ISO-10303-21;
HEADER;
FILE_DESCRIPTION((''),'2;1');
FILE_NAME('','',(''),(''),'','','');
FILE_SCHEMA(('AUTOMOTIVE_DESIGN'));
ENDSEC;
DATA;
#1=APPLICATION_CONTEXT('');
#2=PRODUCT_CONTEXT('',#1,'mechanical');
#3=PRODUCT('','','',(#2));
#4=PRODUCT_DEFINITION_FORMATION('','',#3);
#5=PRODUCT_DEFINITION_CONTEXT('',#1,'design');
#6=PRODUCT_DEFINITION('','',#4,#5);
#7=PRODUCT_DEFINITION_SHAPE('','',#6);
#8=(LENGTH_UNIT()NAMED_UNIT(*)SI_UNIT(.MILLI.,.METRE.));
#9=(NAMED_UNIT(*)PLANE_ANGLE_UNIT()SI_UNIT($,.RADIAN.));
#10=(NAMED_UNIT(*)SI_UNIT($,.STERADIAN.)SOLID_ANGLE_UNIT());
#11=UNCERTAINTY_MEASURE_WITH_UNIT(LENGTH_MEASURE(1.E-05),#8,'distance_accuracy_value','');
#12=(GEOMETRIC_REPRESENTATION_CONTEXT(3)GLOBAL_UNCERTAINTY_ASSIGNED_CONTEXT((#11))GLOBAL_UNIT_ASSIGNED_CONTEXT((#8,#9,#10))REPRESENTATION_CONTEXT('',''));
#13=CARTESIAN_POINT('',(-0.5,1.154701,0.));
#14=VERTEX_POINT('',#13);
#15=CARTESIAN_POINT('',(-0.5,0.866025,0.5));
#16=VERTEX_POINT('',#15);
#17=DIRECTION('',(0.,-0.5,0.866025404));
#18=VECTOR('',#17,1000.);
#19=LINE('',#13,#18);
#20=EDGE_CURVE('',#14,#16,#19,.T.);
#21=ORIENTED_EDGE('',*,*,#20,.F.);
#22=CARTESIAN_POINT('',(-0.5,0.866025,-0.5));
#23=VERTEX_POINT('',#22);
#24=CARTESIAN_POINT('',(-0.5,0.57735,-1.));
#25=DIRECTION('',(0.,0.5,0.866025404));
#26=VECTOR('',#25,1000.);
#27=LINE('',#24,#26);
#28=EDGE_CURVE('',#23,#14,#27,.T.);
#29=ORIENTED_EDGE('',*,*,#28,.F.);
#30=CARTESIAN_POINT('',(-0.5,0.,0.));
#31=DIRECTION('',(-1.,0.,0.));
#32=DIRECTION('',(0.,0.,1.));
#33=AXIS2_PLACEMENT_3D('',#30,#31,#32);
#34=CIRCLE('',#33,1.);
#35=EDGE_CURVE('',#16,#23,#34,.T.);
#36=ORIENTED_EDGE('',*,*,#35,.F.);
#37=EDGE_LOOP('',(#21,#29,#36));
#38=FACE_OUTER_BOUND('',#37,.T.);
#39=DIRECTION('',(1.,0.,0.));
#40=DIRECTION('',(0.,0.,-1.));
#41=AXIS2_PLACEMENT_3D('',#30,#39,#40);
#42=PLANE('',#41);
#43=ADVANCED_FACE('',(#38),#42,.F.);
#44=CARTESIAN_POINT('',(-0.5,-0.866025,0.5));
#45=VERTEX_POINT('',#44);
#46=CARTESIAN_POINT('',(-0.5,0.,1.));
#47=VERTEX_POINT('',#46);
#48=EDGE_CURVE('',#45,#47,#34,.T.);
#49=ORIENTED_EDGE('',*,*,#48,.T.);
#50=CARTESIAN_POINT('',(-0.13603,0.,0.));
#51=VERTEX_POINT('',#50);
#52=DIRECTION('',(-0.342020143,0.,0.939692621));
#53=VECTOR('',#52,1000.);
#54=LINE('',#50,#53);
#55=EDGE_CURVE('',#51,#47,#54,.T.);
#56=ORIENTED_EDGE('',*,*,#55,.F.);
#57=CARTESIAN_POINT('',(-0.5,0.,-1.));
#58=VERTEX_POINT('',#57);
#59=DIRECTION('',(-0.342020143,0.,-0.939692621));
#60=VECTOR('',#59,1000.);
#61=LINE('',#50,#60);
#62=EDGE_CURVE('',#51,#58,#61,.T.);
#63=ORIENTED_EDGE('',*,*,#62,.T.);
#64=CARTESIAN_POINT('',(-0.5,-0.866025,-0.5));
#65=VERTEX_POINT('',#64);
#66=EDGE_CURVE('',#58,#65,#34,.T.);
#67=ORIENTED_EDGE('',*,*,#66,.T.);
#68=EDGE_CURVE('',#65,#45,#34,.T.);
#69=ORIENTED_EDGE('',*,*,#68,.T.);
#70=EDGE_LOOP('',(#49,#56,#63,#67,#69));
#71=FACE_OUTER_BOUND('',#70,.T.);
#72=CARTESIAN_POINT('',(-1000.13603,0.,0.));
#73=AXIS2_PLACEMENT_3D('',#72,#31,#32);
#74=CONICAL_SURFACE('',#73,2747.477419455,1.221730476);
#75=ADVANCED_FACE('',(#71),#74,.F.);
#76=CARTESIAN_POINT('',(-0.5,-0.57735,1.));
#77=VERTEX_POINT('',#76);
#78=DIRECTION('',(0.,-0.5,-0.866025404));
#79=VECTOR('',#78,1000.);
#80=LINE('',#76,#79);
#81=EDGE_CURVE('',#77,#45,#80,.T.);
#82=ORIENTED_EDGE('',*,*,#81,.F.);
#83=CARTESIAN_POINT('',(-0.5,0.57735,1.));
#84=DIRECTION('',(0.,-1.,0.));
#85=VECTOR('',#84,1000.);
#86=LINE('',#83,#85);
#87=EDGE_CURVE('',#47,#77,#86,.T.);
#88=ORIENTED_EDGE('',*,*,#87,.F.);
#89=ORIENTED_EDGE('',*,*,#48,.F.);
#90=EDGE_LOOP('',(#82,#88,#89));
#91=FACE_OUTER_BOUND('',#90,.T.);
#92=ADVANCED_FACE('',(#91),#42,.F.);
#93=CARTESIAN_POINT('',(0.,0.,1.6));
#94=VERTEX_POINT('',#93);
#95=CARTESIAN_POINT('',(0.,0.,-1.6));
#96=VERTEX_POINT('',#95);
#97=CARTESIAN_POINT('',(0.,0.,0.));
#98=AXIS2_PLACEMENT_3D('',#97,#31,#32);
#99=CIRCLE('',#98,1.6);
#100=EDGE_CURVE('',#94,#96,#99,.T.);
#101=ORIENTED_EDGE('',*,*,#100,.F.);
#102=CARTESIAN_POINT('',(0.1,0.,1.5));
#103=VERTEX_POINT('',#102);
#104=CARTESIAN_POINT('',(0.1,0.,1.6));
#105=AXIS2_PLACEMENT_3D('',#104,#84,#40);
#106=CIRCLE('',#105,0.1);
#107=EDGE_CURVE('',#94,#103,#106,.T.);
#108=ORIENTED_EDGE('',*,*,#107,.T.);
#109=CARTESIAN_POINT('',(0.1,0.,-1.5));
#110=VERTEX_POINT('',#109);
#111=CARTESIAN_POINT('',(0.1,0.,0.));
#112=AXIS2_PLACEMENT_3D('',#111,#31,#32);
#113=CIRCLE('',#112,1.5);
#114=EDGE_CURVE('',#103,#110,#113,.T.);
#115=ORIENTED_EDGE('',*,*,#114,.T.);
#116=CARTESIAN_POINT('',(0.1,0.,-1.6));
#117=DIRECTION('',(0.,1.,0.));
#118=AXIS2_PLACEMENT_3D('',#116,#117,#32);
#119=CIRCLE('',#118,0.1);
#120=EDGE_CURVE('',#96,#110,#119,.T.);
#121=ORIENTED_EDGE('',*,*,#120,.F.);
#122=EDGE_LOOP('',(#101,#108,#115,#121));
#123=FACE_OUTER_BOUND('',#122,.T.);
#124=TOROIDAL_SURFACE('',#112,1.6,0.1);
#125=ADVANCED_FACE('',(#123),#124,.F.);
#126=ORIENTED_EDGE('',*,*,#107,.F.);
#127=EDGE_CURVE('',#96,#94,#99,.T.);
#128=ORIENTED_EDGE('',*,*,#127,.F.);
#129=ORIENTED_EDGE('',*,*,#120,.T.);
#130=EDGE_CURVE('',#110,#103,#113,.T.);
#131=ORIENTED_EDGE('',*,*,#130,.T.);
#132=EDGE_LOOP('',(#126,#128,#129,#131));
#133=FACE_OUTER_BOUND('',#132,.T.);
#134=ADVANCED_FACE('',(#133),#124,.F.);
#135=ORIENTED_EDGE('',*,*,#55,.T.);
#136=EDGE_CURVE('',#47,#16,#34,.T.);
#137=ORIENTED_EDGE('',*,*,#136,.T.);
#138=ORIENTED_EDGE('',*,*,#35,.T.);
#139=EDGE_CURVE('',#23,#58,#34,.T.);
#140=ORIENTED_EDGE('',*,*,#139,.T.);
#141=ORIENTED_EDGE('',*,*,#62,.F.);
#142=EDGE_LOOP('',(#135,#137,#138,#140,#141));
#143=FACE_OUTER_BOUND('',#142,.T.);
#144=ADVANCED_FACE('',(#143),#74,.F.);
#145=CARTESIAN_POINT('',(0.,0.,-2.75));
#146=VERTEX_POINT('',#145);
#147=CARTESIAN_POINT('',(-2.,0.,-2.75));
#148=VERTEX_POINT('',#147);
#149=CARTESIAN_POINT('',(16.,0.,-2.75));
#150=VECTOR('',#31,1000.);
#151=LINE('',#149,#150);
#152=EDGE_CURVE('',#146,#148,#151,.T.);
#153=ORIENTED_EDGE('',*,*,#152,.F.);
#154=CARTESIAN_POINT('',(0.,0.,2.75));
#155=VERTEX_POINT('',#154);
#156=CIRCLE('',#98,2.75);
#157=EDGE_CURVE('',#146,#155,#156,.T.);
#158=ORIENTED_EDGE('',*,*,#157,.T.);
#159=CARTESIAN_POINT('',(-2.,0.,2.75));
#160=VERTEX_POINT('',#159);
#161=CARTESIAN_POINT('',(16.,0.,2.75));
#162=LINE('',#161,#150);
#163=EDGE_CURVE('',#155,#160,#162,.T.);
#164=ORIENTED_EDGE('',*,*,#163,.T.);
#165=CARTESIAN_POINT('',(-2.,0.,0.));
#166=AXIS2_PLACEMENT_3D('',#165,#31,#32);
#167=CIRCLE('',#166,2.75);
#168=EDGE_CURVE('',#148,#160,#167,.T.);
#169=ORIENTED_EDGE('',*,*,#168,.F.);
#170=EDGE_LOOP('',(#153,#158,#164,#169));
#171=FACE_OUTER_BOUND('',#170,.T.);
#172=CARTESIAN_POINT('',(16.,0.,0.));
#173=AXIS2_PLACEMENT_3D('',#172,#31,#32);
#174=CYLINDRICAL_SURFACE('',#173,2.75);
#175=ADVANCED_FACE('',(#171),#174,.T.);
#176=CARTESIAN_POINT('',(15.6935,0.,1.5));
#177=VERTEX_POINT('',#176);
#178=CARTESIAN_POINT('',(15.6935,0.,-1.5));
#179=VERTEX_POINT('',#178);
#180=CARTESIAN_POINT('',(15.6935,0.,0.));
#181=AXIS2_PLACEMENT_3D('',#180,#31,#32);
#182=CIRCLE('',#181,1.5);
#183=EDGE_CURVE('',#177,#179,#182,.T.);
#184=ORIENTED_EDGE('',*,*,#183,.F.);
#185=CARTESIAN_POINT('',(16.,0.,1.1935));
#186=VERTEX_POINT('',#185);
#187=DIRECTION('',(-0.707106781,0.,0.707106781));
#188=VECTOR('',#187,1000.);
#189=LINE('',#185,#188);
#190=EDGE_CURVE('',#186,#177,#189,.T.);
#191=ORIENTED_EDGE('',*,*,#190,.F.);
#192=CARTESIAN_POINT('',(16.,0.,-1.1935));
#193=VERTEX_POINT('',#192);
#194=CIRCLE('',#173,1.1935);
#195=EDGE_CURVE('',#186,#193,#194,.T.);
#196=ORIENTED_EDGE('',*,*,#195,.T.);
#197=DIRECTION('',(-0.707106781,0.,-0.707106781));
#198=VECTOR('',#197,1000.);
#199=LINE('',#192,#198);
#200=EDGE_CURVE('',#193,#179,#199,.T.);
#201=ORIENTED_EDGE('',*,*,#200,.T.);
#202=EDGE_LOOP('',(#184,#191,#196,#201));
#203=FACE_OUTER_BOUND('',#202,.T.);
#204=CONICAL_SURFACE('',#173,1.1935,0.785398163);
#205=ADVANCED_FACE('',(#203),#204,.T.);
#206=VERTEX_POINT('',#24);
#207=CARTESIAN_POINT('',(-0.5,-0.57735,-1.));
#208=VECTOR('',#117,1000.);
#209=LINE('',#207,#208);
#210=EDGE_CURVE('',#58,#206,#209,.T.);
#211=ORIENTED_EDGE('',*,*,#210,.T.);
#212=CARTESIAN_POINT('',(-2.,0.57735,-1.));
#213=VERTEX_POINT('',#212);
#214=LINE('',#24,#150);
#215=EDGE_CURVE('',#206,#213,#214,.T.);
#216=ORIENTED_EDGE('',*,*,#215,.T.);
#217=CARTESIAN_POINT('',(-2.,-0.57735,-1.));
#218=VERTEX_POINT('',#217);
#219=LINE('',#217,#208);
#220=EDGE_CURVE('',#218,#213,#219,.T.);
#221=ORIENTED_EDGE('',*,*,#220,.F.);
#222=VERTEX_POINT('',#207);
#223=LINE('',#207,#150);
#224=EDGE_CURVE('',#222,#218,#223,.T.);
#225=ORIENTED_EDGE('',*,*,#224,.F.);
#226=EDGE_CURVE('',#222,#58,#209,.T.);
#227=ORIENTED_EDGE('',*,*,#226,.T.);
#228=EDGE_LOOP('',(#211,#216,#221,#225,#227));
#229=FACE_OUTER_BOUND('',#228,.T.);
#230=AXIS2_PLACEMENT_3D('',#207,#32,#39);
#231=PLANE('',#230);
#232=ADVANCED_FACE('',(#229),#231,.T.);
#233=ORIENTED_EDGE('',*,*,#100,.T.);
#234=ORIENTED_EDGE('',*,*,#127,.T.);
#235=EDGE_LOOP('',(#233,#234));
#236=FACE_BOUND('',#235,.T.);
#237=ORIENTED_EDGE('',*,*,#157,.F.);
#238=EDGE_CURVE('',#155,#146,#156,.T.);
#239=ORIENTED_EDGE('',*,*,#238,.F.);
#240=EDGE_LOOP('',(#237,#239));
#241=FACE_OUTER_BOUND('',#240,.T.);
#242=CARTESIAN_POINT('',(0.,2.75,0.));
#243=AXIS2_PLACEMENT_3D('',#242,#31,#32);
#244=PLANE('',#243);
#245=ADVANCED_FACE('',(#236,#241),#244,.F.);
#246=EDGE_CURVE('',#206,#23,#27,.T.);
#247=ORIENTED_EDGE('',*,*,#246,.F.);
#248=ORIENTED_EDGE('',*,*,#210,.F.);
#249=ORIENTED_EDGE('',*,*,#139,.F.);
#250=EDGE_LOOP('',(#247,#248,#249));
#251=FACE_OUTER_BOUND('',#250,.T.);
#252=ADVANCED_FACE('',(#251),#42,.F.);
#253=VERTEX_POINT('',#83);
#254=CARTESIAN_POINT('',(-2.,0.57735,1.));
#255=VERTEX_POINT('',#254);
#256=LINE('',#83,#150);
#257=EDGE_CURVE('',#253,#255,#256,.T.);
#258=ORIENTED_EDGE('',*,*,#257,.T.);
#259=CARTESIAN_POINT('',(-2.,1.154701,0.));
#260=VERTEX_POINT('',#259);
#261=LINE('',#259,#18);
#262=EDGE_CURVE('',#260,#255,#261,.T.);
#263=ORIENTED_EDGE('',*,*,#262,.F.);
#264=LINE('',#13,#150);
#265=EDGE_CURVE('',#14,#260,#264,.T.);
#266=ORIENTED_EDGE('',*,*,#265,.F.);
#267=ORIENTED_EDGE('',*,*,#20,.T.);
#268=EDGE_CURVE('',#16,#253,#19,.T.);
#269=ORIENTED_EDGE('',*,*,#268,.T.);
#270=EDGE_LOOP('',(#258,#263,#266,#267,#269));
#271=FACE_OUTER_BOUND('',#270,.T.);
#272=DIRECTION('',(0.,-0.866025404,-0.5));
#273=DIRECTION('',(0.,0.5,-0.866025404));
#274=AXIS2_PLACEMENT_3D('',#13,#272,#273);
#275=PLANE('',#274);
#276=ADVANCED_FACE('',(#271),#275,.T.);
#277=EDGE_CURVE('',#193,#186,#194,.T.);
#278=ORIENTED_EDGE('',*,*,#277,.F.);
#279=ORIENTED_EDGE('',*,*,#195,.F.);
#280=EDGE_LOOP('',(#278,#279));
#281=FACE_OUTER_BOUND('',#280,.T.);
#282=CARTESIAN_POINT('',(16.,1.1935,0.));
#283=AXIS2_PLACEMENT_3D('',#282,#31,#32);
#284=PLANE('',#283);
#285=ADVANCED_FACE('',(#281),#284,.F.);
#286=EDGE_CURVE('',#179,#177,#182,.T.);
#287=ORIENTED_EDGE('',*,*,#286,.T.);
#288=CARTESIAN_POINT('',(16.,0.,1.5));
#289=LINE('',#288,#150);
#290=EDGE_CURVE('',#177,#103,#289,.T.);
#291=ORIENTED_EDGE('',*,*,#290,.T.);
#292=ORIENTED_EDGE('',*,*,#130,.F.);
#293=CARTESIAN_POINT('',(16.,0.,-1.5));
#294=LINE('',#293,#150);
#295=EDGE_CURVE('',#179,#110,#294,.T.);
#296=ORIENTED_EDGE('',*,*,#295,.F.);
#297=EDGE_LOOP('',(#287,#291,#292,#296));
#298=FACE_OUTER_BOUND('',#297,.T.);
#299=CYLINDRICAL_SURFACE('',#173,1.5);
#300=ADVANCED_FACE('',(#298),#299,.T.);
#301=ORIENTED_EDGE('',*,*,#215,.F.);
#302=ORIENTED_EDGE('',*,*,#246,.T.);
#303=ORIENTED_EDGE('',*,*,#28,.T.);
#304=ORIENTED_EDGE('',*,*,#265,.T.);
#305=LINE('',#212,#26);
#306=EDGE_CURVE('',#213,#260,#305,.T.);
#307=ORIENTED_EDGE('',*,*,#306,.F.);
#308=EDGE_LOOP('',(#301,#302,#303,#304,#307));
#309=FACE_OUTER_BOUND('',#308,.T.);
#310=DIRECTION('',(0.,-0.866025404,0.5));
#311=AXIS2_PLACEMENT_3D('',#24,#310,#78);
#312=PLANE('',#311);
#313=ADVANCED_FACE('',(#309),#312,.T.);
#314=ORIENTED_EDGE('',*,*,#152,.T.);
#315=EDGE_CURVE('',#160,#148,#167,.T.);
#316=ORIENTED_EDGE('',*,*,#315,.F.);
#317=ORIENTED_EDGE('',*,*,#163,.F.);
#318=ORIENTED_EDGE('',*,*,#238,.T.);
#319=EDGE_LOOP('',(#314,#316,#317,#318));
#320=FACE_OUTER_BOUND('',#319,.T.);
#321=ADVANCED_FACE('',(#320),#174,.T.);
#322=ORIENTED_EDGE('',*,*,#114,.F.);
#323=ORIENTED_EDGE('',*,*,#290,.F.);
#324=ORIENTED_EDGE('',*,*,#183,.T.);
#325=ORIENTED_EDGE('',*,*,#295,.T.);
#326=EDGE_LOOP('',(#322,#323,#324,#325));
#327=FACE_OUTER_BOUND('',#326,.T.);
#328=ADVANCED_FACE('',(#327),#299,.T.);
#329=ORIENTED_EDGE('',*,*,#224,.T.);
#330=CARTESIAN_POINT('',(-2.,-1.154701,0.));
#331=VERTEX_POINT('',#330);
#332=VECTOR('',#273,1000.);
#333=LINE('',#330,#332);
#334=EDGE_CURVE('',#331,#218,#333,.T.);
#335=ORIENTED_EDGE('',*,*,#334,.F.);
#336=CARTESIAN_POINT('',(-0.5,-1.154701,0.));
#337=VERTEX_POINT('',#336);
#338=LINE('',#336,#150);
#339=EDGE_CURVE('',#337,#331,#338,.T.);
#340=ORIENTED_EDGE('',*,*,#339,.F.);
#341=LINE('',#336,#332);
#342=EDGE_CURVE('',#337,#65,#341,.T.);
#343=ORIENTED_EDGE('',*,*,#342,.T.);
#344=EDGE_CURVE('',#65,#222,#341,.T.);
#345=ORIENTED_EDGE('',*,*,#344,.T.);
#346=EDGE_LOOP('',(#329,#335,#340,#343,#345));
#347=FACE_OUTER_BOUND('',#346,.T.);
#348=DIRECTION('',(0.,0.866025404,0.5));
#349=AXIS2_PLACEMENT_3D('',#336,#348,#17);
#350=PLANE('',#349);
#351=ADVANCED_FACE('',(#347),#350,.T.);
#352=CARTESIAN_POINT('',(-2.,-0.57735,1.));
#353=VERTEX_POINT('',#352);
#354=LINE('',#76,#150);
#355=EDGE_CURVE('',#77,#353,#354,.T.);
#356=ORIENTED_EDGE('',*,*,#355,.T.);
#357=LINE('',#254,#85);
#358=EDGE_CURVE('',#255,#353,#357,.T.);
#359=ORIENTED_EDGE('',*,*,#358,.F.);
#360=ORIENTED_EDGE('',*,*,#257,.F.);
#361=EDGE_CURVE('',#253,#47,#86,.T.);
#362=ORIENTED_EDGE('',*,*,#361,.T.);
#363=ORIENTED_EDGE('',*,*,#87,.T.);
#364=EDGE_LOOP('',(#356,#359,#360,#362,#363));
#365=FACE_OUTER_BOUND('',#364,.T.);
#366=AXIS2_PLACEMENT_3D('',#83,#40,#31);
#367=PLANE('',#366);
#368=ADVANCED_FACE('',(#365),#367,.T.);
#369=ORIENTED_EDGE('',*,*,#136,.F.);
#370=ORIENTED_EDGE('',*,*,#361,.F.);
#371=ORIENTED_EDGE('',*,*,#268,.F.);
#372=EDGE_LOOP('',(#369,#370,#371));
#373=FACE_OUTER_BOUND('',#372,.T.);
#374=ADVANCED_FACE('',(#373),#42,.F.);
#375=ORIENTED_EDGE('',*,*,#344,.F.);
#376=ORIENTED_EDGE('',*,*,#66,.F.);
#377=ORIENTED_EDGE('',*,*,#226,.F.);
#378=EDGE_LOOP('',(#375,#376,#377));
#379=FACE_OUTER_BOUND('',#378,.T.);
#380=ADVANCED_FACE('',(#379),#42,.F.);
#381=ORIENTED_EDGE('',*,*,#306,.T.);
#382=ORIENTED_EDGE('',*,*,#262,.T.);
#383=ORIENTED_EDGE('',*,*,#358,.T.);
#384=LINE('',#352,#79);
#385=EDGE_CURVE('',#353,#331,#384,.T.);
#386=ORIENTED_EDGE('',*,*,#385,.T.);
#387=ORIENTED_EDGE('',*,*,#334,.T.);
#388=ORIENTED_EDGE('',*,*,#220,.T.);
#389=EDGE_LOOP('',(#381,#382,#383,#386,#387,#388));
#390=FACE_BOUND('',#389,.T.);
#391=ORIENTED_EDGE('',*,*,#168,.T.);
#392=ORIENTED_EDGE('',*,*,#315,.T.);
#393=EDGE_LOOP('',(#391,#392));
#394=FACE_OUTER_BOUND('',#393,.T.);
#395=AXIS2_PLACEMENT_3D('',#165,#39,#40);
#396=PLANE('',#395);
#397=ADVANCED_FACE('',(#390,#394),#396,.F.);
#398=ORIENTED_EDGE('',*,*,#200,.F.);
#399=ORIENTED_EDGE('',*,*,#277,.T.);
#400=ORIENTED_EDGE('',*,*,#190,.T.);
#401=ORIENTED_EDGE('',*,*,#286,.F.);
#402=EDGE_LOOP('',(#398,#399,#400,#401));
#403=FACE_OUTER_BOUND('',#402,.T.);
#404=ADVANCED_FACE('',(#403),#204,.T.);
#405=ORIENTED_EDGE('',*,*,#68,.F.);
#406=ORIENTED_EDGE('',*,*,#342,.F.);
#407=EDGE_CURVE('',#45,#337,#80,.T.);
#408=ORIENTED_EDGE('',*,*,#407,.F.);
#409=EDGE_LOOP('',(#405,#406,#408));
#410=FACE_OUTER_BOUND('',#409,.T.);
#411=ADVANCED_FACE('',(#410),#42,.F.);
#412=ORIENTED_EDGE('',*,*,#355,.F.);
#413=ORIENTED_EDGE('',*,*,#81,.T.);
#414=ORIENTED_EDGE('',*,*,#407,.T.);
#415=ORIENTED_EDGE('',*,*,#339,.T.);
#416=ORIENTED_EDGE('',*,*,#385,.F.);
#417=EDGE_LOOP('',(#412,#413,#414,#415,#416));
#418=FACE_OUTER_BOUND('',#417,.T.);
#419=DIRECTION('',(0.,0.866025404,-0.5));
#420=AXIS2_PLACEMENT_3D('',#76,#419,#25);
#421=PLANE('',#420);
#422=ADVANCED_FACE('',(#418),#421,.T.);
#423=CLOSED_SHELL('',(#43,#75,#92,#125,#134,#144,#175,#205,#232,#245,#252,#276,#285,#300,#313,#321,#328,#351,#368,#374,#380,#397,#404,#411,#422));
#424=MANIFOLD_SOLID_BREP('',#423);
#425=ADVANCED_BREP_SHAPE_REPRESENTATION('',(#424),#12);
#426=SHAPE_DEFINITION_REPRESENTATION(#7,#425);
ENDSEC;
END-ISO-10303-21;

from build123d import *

# Parameters (mm, degrees)
CUT_EXTRUDE1_DEPTH = 1.5


with BuildPart() as part:
    # Sketch1 → Revolve1 (revolve)
    with BuildSketch(Plane.XY, mode=Mode.PRIVATE) as revolve1_sk:
        with BuildLine():
            Line((-2, 0), (-2, 2.75))
            Line((-2, 2.75), (0, 2.75))
            Line((0, 2.75), (0, 1.6))
            ThreePointArc((0, 1.6), (0.029289322, 1.529289322), (0.1, 1.5))
            Line((0.1, 1.5), (15.6935, 1.5))
            Line((15.6935, 1.5), (16, 1.1935))
            Line((16, 1.1935), (16, 0))
            Line((16, 0), (-2, 0))
        make_face()
    revolve(revolve1_sk.sketch.rotate(Axis((16, 0, 0), (-1, 0, 0)), 270), axis=Axis((16, 0, 0), (-1, 0, 0)))

    # Sketch2 → Cut-Revolve1 (revolve, cut)
    with BuildSketch(Plane.XY, mode=Mode.PRIVATE) as cut_revolve1_sk:
        Polygon((-2, 0), (-2, 1), (-0.5, 1), (-0.136029766, 0), align=None)
    revolve(cut_revolve1_sk.sketch.rotate(Axis((0, 0, 0), (-1, 0, 0)), 270), axis=Axis((0, 0, 0), (-1, 0, 0)), mode=Mode.SUBTRACT)

    # Sketch3 → Cut-Extrude1 (cut)
    with BuildSketch(Plane(origin=(-2, 0, 0), x_dir=(0, 0, -1), z_dir=(1, 0, 0))):
        Polygon((-1, 0.577350269), (-1, -0.577350269), (0, -1.154700538), (1, -0.577350269), (1, 0.577350269), (0, 1.154700538), align=None)
    extrude(amount=CUT_EXTRUDE1_DEPTH, mode=Mode.SUBTRACT)


solid = part.part
